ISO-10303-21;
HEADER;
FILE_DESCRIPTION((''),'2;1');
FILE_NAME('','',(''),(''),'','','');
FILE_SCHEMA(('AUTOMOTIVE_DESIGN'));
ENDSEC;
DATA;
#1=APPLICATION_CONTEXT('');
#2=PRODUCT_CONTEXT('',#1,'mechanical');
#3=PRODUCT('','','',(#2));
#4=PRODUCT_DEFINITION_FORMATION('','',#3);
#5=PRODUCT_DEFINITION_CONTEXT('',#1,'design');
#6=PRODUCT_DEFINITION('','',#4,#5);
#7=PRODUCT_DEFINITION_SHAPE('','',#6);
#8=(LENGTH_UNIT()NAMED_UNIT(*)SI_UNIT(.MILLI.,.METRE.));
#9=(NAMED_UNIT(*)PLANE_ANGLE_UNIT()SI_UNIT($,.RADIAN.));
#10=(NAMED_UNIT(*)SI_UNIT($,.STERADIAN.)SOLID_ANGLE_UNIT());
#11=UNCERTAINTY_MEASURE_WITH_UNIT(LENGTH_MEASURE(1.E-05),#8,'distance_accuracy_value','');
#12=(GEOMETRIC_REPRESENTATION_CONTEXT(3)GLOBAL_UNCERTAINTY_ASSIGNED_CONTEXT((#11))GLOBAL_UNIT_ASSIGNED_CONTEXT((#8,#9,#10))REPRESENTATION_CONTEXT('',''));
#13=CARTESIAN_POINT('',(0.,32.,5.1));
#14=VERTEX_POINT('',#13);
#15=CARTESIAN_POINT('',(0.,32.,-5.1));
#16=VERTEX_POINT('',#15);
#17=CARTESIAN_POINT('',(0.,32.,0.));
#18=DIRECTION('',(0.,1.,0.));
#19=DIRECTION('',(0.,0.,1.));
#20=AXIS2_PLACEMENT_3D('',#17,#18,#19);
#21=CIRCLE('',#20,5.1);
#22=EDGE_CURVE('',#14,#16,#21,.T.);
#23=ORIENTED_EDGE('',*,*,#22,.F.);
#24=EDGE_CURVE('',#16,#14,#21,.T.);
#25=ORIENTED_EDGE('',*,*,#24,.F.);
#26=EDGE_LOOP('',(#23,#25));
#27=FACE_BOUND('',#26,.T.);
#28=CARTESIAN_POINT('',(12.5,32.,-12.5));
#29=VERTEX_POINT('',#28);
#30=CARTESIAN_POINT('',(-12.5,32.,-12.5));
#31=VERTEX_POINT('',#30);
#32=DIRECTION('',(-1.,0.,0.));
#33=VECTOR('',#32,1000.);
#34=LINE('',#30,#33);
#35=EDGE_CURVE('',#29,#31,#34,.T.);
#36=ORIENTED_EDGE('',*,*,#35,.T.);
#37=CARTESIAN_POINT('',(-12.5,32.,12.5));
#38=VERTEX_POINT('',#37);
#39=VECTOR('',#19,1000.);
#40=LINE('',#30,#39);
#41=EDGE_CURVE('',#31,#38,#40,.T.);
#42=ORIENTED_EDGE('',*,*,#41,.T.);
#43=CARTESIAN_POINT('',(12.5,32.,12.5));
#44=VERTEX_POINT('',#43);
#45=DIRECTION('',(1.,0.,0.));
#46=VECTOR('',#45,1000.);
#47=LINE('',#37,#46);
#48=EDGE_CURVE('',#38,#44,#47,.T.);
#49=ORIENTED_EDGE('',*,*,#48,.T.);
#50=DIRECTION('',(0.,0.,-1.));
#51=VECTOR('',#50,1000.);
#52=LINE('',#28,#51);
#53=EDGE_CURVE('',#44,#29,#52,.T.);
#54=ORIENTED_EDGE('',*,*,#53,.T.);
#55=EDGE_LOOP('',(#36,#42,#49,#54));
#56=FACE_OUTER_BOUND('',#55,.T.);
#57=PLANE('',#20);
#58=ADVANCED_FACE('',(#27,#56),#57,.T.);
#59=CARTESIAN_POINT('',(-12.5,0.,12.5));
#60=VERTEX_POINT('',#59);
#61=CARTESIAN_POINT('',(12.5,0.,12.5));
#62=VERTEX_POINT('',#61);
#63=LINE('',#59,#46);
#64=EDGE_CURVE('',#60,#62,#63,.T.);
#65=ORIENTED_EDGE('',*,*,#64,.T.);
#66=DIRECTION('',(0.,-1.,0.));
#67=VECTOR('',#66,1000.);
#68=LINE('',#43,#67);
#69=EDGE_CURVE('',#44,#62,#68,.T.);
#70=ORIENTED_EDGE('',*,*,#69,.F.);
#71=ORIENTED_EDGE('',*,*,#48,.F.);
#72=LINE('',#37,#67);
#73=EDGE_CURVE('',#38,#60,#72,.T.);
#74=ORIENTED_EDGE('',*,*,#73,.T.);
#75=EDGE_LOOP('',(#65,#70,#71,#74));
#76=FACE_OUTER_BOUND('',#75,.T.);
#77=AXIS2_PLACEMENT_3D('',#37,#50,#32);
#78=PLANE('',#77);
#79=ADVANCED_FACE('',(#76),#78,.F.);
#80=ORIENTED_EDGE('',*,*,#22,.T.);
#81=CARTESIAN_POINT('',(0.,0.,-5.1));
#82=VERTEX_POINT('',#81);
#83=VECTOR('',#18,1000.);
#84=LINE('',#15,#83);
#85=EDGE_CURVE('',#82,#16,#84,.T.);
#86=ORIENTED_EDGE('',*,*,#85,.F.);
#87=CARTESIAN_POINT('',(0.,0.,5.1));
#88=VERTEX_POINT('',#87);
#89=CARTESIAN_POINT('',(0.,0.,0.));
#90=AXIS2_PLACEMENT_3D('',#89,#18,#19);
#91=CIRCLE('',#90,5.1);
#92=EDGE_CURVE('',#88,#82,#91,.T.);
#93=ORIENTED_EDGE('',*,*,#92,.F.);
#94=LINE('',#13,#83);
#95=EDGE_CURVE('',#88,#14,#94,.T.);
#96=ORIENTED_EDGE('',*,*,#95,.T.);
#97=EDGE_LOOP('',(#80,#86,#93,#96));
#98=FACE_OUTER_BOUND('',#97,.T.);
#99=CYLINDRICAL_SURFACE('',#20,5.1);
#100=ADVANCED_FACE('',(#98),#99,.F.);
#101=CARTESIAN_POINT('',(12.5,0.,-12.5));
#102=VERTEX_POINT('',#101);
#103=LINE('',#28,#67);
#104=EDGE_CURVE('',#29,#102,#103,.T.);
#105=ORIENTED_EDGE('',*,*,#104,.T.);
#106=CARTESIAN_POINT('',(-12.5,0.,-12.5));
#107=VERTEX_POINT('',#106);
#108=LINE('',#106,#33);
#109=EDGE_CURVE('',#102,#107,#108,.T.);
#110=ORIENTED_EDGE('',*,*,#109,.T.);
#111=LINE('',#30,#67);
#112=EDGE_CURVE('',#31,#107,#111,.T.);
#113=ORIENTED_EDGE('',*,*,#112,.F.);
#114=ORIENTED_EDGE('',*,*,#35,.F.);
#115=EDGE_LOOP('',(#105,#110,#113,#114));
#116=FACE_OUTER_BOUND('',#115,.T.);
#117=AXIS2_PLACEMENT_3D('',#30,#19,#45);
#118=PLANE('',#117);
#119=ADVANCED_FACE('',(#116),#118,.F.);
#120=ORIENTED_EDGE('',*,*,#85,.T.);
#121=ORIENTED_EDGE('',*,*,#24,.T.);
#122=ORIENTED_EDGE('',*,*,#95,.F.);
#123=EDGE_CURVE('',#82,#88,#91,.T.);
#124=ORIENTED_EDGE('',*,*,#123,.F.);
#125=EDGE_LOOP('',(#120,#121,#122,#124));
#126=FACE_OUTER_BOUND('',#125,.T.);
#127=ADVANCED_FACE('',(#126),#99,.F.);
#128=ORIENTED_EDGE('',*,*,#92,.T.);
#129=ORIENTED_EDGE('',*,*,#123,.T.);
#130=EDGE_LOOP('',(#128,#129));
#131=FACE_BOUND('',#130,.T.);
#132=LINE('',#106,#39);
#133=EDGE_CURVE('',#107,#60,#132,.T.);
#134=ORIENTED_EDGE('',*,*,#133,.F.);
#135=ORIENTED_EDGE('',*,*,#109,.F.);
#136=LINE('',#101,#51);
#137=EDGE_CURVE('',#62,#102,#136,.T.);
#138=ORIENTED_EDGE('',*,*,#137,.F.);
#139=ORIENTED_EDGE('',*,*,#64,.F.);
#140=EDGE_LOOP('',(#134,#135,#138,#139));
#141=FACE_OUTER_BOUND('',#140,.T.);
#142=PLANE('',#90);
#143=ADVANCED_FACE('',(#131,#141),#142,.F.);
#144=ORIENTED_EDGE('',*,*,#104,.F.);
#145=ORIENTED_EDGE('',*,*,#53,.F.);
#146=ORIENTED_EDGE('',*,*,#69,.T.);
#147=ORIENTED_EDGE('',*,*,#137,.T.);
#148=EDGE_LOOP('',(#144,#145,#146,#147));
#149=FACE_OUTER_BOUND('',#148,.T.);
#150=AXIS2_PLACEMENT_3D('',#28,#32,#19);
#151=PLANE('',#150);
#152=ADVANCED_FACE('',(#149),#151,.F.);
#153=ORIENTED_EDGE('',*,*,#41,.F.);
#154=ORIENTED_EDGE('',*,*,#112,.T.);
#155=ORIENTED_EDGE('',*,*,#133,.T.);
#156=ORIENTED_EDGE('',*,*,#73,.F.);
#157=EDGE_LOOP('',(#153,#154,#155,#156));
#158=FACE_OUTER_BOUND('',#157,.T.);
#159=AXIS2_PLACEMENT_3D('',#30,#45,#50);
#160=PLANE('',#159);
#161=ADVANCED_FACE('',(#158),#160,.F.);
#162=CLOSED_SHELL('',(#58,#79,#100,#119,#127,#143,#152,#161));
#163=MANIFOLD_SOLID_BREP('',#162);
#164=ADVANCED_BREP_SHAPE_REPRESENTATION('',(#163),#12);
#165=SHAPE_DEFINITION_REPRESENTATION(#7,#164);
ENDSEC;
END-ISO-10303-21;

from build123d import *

# Parameters (mm, degrees)
SKETCH1_W           = 25
SKETCH1_H           = 25
BOSS_EXTRUDE1_DEPTH = 32
M12_TAPPED_HOLE1_D  = 10.2


with BuildPart() as part:
    # Sketch1 → Boss-Extrude1 (new body)
    with BuildSketch(Plane(origin=(0, 0, 0), x_dir=(1, 0, 0), z_dir=(0, 1, 0))):
        Rectangle(SKETCH1_W, SKETCH1_H)
    extrude(amount=BOSS_EXTRUDE1_DEPTH)

    # M12 Tapped Hole1 (through all)
    with Locations(Plane(origin=(0, 32, 0), x_dir=(1, 0, 0), z_dir=(0, 1, 0))):
        with Locations((0, 0)):
            Hole(M12_TAPPED_HOLE1_D / 2)


solid = part.part
